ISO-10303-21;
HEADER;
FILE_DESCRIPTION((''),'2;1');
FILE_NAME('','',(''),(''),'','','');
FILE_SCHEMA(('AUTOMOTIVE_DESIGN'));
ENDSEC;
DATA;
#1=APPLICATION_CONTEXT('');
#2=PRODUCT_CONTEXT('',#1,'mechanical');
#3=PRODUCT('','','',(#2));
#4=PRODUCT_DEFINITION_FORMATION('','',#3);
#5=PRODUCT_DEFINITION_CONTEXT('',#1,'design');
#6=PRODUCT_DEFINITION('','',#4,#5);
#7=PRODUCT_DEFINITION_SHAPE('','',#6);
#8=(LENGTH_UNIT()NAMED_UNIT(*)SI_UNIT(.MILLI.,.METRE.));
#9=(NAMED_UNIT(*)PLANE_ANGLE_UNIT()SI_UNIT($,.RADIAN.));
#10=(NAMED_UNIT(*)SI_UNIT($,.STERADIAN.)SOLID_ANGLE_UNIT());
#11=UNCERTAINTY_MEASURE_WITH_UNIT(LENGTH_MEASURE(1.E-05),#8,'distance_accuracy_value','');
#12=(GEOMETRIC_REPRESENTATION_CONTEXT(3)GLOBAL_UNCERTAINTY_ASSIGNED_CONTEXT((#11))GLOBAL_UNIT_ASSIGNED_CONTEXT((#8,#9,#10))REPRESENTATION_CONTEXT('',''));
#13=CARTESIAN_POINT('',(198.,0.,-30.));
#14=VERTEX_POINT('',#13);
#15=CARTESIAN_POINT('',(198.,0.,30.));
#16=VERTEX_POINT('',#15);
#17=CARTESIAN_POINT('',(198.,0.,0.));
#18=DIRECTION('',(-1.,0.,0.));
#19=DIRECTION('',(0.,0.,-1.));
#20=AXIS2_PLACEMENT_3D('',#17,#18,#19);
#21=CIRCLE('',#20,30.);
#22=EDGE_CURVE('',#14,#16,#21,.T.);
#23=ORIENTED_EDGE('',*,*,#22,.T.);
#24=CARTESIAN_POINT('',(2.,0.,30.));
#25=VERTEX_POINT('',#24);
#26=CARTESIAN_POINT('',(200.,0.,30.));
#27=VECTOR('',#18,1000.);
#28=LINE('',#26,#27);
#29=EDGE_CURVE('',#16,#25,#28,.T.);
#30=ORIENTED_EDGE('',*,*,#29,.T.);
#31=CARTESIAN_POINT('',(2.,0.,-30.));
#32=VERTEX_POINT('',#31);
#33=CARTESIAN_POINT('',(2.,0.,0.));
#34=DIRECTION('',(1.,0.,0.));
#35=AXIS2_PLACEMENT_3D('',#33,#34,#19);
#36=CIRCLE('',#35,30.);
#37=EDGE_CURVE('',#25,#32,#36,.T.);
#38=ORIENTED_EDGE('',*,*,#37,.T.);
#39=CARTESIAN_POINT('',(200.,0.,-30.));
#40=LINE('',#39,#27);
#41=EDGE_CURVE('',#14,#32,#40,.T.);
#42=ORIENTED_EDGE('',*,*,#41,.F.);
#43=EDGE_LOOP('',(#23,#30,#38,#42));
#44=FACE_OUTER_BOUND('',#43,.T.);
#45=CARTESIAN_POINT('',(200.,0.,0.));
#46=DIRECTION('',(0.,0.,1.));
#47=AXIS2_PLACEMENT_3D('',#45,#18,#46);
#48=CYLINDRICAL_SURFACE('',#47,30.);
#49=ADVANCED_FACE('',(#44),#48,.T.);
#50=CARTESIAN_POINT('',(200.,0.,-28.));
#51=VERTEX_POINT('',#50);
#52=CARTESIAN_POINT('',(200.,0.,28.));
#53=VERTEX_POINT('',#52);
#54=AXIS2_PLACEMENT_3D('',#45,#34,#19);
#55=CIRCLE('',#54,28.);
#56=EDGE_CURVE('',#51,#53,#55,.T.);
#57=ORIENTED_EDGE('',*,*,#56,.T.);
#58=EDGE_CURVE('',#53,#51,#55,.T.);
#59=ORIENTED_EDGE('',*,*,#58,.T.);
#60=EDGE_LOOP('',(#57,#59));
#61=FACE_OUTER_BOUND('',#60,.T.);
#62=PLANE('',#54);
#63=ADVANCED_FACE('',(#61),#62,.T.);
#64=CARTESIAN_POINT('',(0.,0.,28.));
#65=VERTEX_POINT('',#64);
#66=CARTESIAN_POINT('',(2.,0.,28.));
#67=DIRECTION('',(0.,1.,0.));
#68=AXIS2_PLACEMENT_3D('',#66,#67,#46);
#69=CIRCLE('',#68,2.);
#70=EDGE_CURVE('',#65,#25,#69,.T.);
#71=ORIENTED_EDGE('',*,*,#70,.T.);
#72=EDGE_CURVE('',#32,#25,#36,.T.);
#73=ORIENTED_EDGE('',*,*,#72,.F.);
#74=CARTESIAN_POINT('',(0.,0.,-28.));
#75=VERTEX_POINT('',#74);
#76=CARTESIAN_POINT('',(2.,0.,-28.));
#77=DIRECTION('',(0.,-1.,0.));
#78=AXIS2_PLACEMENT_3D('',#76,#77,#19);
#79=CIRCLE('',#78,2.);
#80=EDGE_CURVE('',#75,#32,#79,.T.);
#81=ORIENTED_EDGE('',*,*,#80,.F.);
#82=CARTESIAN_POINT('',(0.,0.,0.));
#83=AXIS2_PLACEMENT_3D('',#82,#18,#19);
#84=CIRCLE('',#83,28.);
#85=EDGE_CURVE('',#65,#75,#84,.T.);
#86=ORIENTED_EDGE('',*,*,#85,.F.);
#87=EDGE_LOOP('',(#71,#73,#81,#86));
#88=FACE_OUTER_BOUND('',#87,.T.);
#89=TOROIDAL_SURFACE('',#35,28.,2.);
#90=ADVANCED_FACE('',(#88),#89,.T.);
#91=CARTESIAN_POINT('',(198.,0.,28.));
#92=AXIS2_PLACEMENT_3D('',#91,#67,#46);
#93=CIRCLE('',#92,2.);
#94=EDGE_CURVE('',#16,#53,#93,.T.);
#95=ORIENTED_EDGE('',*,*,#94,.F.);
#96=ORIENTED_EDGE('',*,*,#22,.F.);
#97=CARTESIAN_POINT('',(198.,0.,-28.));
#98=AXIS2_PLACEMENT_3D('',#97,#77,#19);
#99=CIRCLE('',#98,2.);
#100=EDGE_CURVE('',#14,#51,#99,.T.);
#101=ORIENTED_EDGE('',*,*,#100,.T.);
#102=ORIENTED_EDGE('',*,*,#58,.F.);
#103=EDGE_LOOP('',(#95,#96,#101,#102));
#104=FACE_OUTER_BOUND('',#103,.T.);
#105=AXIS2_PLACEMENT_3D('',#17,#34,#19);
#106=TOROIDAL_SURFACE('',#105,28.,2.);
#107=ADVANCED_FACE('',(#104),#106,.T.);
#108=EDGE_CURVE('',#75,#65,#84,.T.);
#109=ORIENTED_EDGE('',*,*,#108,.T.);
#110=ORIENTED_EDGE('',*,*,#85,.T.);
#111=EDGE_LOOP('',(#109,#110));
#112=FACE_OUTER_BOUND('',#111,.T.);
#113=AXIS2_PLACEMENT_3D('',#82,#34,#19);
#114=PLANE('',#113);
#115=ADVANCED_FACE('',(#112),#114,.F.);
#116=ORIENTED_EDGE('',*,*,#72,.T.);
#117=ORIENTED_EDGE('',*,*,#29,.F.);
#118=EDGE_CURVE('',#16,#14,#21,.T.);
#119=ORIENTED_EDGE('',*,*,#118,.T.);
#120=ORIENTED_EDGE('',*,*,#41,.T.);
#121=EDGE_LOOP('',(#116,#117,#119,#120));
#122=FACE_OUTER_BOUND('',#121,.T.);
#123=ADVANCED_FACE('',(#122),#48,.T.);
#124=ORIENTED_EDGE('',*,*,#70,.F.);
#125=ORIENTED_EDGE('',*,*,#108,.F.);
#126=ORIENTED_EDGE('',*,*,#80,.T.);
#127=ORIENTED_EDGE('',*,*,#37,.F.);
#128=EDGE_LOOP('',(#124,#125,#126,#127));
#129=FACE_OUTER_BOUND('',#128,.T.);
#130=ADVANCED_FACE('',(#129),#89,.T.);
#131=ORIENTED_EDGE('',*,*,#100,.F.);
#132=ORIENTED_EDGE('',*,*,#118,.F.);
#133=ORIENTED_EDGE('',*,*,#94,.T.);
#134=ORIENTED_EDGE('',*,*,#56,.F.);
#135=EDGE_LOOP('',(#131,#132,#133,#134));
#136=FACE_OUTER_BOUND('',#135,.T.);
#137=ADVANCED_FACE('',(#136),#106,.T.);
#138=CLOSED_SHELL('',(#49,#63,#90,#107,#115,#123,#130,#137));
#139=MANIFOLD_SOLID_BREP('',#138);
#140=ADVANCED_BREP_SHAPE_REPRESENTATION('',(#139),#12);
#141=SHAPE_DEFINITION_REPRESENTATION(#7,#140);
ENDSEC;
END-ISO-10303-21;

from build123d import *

# Parameters (mm, degrees)
SKETCH1_R           = 30
BOSS_EXTRUDE1_DEPTH = 200
FILLET1_R           = 2


with BuildPart() as part:
    # Sketch1 → Boss-Extrude1 (new body)
    with BuildSketch(Plane(origin=(0, 0, 0), x_dir=(0, 0, -1), z_dir=(1, 0, 0))):
        Circle(SKETCH1_R)
    extrude(amount=BOSS_EXTRUDE1_DEPTH)

    # Fillet1
    fillet1_edges = [part.edges().sort_by_distance(p)[0] for p in [
        (0, 0, 30),
        (200, 0, 30),
    ]]
    fillet(fillet1_edges, radius=FILLET1_R)


solid = part.part
